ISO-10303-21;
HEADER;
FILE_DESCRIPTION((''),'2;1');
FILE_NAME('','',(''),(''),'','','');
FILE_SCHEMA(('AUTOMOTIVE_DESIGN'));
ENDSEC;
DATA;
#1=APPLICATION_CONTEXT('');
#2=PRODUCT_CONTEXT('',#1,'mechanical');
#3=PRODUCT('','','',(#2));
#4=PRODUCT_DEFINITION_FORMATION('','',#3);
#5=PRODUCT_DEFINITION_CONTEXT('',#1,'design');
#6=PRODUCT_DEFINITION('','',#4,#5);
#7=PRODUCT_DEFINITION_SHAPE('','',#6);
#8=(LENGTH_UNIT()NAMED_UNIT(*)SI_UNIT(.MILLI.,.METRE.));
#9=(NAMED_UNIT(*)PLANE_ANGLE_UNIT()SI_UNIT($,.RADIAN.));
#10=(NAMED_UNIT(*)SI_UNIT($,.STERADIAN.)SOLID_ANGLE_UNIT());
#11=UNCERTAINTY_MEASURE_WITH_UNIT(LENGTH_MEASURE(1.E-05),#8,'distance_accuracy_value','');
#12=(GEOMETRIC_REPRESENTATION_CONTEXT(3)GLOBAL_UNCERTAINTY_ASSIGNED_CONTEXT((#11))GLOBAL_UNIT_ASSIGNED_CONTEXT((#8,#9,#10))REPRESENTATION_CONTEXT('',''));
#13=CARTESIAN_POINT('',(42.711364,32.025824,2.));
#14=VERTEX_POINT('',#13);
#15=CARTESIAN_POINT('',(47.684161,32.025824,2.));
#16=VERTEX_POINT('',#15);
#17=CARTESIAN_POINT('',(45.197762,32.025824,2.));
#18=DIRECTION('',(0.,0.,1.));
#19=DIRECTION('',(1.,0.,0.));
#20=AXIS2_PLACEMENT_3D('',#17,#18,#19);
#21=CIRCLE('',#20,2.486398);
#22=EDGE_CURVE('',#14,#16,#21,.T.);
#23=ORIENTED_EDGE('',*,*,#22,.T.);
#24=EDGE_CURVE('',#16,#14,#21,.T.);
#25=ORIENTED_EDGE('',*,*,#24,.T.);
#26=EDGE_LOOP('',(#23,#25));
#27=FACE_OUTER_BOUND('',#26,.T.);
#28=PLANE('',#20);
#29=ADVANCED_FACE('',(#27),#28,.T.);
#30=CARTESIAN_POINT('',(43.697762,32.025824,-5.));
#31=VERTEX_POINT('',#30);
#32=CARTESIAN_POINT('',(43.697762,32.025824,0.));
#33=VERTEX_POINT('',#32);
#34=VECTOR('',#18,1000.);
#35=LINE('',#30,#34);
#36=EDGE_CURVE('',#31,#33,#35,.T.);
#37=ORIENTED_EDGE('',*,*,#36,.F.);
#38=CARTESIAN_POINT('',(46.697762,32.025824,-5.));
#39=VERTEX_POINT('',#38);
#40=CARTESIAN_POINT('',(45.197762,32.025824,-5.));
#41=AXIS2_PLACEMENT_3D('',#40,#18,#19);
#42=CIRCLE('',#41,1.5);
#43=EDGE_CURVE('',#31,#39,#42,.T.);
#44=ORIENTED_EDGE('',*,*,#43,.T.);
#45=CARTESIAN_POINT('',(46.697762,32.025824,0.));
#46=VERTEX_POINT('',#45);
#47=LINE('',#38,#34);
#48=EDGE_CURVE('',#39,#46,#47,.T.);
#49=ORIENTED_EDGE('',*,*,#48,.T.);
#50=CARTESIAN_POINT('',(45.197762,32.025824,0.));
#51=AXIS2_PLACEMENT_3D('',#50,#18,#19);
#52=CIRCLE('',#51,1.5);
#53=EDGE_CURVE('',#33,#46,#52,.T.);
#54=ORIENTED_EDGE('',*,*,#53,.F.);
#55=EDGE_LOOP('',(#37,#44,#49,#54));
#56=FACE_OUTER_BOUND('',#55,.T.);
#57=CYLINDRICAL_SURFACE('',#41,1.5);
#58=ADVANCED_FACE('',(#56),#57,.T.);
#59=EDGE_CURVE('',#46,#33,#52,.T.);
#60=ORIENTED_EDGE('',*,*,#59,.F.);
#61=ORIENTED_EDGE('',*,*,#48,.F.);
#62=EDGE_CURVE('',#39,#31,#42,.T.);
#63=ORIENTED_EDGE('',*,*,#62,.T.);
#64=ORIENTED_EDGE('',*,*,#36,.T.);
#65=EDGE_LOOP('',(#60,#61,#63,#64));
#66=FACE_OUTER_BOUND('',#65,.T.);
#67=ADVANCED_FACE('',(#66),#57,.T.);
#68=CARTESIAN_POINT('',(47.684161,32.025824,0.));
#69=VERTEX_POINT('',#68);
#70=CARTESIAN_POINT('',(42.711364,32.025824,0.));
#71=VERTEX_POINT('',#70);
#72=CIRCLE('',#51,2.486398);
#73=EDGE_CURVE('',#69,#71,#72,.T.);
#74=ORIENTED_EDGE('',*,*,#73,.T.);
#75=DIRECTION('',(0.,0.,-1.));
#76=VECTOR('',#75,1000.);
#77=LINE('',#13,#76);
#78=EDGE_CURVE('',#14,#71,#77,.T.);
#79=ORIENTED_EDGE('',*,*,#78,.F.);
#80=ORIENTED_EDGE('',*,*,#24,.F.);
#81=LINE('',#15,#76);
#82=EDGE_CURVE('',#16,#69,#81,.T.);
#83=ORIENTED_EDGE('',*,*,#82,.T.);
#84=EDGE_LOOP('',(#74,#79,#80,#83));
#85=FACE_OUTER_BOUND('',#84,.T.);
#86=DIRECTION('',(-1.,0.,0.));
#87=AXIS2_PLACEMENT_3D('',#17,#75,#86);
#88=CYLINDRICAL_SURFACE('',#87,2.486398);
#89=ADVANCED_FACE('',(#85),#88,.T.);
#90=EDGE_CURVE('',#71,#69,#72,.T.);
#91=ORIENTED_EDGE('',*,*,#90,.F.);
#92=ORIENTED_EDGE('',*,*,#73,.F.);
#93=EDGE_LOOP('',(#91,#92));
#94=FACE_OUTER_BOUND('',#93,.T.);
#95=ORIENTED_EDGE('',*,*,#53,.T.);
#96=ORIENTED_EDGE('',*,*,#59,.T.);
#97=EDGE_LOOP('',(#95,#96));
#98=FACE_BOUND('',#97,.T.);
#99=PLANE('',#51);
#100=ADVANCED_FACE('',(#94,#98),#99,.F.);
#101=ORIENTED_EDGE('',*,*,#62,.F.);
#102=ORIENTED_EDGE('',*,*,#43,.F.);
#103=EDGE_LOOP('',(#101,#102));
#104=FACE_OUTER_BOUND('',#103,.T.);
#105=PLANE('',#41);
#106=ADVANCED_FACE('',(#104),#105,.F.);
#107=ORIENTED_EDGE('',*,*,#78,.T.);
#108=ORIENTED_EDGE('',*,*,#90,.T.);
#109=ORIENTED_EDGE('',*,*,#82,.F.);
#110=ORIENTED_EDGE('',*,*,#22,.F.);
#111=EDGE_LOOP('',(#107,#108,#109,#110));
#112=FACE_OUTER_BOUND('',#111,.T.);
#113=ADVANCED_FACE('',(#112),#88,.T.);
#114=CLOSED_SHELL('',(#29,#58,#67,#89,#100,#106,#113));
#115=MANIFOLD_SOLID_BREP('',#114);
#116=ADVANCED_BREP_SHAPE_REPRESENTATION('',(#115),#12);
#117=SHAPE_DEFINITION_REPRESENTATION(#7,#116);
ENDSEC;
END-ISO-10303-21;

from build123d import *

# Parameters (mm, degrees)
SKETCH1_R           = 1.5
BOSS_EXTRUDE1_DEPTH = 5
SKETCH2_R           = 2.486398422
BOSS_EXTRUDE2_DEPTH = 2


with BuildPart() as part:
    # Sketch1 → Boss-Extrude1 (new body)
    with BuildSketch(Plane.XY):
        with Locations((45.197762361, 32.025823543)):
            Circle(SKETCH1_R)
    extrude(amount=-BOSS_EXTRUDE1_DEPTH)

    # Sketch2 → Boss-Extrude2 (add)
    with BuildSketch(Plane.XY):
        with Locations((45.197762361, 32.025823543)):
            Circle(SKETCH2_R)
    extrude(amount=BOSS_EXTRUDE2_DEPTH)


solid = part.part
